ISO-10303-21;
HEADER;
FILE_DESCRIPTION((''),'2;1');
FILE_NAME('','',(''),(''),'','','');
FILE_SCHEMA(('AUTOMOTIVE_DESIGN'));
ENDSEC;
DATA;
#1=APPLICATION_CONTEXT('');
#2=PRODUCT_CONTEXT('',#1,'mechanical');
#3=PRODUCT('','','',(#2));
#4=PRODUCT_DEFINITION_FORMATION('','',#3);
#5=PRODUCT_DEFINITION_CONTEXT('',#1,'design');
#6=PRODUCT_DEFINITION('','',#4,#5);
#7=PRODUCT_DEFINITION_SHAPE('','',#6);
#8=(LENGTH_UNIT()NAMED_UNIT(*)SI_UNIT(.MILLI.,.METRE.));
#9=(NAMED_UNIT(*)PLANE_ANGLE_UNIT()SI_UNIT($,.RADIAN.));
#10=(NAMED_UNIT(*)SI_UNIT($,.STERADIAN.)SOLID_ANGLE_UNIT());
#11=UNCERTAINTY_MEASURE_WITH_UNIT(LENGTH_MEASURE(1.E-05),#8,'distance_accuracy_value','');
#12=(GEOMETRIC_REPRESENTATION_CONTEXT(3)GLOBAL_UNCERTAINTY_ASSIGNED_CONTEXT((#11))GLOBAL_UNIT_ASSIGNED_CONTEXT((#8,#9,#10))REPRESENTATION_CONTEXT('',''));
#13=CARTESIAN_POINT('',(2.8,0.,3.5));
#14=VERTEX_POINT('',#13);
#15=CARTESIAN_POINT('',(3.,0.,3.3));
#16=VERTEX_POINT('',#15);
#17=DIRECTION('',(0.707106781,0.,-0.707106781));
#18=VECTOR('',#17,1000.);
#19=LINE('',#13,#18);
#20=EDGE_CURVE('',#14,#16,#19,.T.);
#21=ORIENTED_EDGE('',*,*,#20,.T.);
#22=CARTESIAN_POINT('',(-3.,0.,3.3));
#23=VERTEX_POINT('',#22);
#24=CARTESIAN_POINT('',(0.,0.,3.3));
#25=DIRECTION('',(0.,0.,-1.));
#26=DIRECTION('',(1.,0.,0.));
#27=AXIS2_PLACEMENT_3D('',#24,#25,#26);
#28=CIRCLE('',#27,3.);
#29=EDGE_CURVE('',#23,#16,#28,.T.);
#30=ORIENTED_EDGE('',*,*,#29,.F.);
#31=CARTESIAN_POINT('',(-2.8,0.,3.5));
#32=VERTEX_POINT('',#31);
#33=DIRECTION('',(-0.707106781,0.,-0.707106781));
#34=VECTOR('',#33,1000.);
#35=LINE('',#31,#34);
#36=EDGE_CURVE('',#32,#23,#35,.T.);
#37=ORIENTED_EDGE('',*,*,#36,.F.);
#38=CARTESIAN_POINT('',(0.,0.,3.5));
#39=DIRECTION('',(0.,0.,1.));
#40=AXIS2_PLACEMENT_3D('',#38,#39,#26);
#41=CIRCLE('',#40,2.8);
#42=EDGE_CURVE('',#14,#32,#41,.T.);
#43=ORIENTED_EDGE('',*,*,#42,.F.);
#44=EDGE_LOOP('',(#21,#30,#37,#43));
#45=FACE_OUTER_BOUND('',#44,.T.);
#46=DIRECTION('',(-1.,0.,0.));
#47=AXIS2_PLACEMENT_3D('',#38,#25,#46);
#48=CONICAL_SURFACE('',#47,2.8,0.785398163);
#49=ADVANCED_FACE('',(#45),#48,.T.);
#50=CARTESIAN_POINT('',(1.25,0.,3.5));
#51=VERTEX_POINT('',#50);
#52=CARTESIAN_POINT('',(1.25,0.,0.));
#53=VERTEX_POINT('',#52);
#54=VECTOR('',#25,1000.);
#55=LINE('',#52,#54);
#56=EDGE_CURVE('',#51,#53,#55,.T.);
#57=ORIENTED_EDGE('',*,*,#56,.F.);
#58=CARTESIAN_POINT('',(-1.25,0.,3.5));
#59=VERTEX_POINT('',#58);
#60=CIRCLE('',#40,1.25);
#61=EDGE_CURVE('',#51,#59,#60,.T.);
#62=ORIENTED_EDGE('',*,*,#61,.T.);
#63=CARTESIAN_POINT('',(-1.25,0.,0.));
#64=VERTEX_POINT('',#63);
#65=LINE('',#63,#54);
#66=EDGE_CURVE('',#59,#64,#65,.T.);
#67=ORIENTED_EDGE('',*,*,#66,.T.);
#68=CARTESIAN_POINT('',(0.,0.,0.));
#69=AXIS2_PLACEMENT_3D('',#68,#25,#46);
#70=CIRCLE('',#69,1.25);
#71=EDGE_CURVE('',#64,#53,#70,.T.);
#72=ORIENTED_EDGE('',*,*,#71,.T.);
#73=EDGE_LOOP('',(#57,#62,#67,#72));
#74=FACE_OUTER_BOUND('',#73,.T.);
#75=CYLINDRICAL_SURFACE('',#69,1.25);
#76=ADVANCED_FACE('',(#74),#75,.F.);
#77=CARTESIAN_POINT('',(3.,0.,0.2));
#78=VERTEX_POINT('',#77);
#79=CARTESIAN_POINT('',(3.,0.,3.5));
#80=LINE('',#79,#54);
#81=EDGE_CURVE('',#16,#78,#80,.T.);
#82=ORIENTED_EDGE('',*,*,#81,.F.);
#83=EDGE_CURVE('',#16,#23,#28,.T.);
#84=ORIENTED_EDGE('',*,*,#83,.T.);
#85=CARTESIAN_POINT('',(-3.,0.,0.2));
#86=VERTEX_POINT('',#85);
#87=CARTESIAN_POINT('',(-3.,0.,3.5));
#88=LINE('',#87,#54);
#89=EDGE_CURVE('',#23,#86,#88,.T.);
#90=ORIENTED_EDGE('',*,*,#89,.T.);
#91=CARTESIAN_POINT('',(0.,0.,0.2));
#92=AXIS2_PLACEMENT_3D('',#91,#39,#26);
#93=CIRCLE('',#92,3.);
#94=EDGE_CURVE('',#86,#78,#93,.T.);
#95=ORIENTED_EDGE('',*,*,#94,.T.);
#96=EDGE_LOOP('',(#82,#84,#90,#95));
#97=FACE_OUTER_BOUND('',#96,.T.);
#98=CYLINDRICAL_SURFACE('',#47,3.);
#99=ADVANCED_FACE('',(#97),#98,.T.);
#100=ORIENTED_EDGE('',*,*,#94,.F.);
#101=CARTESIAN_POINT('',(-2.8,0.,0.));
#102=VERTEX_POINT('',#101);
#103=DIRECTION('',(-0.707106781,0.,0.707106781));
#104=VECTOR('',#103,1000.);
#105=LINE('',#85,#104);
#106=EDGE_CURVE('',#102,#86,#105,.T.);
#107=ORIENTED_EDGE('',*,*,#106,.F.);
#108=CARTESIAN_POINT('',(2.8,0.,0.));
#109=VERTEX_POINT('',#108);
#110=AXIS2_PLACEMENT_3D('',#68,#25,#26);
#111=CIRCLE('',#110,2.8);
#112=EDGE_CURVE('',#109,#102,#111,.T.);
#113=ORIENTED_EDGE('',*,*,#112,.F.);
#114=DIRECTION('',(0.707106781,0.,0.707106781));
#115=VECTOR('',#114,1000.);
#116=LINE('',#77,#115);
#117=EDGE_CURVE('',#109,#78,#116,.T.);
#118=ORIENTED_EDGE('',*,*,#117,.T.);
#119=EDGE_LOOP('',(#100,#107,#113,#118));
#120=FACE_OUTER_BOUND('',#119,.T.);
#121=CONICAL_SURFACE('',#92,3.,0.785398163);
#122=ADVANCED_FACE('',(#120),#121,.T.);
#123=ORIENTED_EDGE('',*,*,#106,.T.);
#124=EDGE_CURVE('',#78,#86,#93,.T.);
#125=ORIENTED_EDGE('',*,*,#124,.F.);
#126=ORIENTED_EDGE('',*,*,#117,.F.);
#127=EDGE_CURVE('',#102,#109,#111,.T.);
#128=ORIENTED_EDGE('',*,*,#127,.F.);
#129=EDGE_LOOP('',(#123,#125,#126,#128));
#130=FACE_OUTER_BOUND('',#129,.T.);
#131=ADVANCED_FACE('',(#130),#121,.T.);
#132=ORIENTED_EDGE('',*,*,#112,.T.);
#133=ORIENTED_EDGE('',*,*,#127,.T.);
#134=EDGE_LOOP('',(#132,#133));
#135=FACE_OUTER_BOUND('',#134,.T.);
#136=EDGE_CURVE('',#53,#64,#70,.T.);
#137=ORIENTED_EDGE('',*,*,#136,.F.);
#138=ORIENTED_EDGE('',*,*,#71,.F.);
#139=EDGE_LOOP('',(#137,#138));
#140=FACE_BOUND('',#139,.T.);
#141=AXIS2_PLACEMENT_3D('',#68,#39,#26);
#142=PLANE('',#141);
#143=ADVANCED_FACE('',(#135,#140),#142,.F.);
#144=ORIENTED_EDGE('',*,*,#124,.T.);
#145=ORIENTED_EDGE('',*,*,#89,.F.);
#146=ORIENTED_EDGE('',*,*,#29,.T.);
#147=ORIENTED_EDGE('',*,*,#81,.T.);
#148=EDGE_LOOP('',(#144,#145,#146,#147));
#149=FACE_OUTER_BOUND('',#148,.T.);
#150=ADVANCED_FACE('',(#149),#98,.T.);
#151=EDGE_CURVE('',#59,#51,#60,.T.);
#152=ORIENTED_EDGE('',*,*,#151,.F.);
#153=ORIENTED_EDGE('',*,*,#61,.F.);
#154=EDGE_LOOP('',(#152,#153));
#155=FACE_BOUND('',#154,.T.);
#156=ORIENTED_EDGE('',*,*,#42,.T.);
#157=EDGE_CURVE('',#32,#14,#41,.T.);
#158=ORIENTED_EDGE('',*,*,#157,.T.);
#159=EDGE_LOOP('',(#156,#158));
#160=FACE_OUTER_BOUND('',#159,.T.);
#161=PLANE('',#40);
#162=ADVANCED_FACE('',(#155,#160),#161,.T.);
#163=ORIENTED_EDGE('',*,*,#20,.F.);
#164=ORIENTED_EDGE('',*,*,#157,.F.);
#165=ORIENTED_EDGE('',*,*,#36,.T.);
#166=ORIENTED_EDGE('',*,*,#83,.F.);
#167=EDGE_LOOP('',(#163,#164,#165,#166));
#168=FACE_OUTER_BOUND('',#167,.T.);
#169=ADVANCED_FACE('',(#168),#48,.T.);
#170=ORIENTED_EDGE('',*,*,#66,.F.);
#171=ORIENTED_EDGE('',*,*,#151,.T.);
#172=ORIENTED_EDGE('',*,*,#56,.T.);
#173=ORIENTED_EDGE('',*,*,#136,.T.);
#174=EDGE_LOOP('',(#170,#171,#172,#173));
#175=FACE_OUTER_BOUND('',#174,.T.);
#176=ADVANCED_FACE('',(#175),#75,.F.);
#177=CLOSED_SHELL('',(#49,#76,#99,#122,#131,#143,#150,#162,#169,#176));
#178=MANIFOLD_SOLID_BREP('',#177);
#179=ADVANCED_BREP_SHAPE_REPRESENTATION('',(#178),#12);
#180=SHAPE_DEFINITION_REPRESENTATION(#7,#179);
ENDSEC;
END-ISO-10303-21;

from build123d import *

# Parameters (mm, degrees)
SKETCH1_R             = 3
BOSS_EXTRUDE1_DEPTH   = 3.5
M3_TAPPED_HOLE1_D     = 2.5
M3_TAPPED_HOLE1_DEPTH = 7.5
CHAMFER1_SIZE         = 0.2


with BuildPart() as part:
    # Sketch1 → Boss-Extrude1 (new body)
    with BuildSketch(Plane.XY):
        Circle(SKETCH1_R)
    extrude(amount=BOSS_EXTRUDE1_DEPTH)

    # M3 Tapped Hole1
    with Locations(Plane(origin=(0, 0, 0), x_dir=(-1, 0, 0), z_dir=(0, 0, -1))):
        with Locations((0, 0)):
            Hole(M3_TAPPED_HOLE1_D / 2, depth=M3_TAPPED_HOLE1_DEPTH)

    # Chamfer1
    chamfer1_edges = [part.edges().sort_by_distance(p)[0] for p in [
        (-3, 0, 0),
        (-3, 0, 3.5),
    ]]
    chamfer(chamfer1_edges, length=CHAMFER1_SIZE)


solid = part.part
